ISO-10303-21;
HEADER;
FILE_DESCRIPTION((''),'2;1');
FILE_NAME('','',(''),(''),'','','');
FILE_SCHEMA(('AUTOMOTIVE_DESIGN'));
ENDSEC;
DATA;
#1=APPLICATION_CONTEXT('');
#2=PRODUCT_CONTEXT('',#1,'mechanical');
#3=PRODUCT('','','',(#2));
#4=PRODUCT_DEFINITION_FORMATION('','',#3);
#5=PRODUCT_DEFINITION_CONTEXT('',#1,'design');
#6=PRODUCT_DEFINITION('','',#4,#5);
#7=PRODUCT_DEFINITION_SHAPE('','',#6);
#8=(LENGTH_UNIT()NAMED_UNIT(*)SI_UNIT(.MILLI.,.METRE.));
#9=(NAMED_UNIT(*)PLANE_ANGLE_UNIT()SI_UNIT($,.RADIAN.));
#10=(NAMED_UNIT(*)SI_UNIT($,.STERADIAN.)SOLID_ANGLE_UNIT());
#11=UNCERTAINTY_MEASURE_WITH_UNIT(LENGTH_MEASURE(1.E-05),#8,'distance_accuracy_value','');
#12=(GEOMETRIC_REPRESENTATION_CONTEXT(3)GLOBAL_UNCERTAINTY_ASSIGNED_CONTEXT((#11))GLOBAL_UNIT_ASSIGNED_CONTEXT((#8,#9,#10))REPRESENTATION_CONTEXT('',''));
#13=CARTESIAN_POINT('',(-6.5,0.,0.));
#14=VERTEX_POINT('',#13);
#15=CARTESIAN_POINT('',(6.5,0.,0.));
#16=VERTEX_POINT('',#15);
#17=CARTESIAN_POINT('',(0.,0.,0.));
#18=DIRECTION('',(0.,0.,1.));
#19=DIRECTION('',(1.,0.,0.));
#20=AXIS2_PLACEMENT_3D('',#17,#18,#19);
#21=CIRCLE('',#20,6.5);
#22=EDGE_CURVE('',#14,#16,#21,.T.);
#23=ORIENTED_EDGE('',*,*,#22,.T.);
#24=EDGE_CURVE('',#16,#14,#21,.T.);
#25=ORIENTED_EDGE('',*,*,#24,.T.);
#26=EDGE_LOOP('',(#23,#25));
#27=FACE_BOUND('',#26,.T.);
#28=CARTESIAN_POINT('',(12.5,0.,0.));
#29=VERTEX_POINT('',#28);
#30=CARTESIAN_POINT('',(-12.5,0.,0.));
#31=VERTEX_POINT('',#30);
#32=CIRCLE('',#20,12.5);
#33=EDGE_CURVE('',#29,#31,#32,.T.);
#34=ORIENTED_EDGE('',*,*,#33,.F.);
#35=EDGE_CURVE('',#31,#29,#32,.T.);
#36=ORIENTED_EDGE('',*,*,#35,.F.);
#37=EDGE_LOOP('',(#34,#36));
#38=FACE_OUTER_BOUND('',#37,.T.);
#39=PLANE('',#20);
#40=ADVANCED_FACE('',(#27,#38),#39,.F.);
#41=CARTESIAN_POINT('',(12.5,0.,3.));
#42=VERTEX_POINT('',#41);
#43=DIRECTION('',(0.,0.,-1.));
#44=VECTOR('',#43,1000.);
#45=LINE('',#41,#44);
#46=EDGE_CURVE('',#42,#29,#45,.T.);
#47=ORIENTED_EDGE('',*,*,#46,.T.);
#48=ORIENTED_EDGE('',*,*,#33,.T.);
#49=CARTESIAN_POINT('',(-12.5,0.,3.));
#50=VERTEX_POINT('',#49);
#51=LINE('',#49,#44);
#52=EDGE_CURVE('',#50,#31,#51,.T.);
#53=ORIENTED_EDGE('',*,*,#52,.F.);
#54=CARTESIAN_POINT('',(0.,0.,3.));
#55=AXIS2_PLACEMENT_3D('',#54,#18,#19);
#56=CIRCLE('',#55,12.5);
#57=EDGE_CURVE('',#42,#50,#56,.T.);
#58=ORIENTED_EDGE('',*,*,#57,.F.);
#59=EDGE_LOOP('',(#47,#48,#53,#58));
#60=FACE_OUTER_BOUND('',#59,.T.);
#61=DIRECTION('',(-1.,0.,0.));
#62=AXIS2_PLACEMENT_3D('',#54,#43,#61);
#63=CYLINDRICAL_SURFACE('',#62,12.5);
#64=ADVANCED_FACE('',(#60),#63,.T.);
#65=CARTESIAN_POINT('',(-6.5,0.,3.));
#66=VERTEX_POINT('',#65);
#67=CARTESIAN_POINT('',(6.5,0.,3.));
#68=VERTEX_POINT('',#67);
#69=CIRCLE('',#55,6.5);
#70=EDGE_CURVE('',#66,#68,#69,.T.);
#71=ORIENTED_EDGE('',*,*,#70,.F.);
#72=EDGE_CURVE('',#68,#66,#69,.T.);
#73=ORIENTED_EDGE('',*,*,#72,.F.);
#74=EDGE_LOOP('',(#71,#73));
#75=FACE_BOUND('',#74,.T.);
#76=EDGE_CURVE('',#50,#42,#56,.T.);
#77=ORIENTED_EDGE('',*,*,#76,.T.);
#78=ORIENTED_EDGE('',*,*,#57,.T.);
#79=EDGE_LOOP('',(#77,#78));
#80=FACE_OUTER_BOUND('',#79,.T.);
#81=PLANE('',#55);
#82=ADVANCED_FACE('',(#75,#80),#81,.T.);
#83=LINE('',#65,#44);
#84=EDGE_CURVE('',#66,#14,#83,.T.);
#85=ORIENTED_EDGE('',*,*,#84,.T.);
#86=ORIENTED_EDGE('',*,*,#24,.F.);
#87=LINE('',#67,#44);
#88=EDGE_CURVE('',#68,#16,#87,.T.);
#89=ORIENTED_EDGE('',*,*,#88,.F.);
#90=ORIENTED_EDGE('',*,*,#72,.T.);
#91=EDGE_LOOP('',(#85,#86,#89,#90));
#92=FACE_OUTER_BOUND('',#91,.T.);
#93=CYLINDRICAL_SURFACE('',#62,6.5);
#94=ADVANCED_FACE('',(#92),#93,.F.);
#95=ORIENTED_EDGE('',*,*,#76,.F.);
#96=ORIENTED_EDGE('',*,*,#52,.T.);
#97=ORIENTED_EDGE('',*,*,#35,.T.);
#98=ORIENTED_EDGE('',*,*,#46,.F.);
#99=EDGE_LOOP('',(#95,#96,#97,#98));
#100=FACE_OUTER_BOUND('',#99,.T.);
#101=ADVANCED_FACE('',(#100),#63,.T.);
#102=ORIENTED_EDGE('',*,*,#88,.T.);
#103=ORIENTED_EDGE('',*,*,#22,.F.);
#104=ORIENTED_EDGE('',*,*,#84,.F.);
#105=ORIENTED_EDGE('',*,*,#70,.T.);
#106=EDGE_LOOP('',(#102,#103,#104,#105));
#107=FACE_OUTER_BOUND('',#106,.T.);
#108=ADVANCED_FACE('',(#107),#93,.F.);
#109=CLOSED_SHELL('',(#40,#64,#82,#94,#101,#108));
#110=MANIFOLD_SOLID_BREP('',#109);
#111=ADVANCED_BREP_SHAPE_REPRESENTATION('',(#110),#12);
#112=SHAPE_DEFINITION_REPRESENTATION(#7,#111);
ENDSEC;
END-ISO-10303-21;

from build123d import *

# Parameters (mm, degrees)
SKETCH1_R           = 12.5
SKETCH1_R_2         = 6.5
BOSS_EXTRUDE1_DEPTH = 3


with BuildPart() as part:
    # Sketch1 → Boss-Extrude1 (new body)
    with BuildSketch(Plane.XY):
        Circle(SKETCH1_R)
        Circle(SKETCH1_R_2, mode=Mode.SUBTRACT)
    extrude(amount=BOSS_EXTRUDE1_DEPTH)


solid = part.part
